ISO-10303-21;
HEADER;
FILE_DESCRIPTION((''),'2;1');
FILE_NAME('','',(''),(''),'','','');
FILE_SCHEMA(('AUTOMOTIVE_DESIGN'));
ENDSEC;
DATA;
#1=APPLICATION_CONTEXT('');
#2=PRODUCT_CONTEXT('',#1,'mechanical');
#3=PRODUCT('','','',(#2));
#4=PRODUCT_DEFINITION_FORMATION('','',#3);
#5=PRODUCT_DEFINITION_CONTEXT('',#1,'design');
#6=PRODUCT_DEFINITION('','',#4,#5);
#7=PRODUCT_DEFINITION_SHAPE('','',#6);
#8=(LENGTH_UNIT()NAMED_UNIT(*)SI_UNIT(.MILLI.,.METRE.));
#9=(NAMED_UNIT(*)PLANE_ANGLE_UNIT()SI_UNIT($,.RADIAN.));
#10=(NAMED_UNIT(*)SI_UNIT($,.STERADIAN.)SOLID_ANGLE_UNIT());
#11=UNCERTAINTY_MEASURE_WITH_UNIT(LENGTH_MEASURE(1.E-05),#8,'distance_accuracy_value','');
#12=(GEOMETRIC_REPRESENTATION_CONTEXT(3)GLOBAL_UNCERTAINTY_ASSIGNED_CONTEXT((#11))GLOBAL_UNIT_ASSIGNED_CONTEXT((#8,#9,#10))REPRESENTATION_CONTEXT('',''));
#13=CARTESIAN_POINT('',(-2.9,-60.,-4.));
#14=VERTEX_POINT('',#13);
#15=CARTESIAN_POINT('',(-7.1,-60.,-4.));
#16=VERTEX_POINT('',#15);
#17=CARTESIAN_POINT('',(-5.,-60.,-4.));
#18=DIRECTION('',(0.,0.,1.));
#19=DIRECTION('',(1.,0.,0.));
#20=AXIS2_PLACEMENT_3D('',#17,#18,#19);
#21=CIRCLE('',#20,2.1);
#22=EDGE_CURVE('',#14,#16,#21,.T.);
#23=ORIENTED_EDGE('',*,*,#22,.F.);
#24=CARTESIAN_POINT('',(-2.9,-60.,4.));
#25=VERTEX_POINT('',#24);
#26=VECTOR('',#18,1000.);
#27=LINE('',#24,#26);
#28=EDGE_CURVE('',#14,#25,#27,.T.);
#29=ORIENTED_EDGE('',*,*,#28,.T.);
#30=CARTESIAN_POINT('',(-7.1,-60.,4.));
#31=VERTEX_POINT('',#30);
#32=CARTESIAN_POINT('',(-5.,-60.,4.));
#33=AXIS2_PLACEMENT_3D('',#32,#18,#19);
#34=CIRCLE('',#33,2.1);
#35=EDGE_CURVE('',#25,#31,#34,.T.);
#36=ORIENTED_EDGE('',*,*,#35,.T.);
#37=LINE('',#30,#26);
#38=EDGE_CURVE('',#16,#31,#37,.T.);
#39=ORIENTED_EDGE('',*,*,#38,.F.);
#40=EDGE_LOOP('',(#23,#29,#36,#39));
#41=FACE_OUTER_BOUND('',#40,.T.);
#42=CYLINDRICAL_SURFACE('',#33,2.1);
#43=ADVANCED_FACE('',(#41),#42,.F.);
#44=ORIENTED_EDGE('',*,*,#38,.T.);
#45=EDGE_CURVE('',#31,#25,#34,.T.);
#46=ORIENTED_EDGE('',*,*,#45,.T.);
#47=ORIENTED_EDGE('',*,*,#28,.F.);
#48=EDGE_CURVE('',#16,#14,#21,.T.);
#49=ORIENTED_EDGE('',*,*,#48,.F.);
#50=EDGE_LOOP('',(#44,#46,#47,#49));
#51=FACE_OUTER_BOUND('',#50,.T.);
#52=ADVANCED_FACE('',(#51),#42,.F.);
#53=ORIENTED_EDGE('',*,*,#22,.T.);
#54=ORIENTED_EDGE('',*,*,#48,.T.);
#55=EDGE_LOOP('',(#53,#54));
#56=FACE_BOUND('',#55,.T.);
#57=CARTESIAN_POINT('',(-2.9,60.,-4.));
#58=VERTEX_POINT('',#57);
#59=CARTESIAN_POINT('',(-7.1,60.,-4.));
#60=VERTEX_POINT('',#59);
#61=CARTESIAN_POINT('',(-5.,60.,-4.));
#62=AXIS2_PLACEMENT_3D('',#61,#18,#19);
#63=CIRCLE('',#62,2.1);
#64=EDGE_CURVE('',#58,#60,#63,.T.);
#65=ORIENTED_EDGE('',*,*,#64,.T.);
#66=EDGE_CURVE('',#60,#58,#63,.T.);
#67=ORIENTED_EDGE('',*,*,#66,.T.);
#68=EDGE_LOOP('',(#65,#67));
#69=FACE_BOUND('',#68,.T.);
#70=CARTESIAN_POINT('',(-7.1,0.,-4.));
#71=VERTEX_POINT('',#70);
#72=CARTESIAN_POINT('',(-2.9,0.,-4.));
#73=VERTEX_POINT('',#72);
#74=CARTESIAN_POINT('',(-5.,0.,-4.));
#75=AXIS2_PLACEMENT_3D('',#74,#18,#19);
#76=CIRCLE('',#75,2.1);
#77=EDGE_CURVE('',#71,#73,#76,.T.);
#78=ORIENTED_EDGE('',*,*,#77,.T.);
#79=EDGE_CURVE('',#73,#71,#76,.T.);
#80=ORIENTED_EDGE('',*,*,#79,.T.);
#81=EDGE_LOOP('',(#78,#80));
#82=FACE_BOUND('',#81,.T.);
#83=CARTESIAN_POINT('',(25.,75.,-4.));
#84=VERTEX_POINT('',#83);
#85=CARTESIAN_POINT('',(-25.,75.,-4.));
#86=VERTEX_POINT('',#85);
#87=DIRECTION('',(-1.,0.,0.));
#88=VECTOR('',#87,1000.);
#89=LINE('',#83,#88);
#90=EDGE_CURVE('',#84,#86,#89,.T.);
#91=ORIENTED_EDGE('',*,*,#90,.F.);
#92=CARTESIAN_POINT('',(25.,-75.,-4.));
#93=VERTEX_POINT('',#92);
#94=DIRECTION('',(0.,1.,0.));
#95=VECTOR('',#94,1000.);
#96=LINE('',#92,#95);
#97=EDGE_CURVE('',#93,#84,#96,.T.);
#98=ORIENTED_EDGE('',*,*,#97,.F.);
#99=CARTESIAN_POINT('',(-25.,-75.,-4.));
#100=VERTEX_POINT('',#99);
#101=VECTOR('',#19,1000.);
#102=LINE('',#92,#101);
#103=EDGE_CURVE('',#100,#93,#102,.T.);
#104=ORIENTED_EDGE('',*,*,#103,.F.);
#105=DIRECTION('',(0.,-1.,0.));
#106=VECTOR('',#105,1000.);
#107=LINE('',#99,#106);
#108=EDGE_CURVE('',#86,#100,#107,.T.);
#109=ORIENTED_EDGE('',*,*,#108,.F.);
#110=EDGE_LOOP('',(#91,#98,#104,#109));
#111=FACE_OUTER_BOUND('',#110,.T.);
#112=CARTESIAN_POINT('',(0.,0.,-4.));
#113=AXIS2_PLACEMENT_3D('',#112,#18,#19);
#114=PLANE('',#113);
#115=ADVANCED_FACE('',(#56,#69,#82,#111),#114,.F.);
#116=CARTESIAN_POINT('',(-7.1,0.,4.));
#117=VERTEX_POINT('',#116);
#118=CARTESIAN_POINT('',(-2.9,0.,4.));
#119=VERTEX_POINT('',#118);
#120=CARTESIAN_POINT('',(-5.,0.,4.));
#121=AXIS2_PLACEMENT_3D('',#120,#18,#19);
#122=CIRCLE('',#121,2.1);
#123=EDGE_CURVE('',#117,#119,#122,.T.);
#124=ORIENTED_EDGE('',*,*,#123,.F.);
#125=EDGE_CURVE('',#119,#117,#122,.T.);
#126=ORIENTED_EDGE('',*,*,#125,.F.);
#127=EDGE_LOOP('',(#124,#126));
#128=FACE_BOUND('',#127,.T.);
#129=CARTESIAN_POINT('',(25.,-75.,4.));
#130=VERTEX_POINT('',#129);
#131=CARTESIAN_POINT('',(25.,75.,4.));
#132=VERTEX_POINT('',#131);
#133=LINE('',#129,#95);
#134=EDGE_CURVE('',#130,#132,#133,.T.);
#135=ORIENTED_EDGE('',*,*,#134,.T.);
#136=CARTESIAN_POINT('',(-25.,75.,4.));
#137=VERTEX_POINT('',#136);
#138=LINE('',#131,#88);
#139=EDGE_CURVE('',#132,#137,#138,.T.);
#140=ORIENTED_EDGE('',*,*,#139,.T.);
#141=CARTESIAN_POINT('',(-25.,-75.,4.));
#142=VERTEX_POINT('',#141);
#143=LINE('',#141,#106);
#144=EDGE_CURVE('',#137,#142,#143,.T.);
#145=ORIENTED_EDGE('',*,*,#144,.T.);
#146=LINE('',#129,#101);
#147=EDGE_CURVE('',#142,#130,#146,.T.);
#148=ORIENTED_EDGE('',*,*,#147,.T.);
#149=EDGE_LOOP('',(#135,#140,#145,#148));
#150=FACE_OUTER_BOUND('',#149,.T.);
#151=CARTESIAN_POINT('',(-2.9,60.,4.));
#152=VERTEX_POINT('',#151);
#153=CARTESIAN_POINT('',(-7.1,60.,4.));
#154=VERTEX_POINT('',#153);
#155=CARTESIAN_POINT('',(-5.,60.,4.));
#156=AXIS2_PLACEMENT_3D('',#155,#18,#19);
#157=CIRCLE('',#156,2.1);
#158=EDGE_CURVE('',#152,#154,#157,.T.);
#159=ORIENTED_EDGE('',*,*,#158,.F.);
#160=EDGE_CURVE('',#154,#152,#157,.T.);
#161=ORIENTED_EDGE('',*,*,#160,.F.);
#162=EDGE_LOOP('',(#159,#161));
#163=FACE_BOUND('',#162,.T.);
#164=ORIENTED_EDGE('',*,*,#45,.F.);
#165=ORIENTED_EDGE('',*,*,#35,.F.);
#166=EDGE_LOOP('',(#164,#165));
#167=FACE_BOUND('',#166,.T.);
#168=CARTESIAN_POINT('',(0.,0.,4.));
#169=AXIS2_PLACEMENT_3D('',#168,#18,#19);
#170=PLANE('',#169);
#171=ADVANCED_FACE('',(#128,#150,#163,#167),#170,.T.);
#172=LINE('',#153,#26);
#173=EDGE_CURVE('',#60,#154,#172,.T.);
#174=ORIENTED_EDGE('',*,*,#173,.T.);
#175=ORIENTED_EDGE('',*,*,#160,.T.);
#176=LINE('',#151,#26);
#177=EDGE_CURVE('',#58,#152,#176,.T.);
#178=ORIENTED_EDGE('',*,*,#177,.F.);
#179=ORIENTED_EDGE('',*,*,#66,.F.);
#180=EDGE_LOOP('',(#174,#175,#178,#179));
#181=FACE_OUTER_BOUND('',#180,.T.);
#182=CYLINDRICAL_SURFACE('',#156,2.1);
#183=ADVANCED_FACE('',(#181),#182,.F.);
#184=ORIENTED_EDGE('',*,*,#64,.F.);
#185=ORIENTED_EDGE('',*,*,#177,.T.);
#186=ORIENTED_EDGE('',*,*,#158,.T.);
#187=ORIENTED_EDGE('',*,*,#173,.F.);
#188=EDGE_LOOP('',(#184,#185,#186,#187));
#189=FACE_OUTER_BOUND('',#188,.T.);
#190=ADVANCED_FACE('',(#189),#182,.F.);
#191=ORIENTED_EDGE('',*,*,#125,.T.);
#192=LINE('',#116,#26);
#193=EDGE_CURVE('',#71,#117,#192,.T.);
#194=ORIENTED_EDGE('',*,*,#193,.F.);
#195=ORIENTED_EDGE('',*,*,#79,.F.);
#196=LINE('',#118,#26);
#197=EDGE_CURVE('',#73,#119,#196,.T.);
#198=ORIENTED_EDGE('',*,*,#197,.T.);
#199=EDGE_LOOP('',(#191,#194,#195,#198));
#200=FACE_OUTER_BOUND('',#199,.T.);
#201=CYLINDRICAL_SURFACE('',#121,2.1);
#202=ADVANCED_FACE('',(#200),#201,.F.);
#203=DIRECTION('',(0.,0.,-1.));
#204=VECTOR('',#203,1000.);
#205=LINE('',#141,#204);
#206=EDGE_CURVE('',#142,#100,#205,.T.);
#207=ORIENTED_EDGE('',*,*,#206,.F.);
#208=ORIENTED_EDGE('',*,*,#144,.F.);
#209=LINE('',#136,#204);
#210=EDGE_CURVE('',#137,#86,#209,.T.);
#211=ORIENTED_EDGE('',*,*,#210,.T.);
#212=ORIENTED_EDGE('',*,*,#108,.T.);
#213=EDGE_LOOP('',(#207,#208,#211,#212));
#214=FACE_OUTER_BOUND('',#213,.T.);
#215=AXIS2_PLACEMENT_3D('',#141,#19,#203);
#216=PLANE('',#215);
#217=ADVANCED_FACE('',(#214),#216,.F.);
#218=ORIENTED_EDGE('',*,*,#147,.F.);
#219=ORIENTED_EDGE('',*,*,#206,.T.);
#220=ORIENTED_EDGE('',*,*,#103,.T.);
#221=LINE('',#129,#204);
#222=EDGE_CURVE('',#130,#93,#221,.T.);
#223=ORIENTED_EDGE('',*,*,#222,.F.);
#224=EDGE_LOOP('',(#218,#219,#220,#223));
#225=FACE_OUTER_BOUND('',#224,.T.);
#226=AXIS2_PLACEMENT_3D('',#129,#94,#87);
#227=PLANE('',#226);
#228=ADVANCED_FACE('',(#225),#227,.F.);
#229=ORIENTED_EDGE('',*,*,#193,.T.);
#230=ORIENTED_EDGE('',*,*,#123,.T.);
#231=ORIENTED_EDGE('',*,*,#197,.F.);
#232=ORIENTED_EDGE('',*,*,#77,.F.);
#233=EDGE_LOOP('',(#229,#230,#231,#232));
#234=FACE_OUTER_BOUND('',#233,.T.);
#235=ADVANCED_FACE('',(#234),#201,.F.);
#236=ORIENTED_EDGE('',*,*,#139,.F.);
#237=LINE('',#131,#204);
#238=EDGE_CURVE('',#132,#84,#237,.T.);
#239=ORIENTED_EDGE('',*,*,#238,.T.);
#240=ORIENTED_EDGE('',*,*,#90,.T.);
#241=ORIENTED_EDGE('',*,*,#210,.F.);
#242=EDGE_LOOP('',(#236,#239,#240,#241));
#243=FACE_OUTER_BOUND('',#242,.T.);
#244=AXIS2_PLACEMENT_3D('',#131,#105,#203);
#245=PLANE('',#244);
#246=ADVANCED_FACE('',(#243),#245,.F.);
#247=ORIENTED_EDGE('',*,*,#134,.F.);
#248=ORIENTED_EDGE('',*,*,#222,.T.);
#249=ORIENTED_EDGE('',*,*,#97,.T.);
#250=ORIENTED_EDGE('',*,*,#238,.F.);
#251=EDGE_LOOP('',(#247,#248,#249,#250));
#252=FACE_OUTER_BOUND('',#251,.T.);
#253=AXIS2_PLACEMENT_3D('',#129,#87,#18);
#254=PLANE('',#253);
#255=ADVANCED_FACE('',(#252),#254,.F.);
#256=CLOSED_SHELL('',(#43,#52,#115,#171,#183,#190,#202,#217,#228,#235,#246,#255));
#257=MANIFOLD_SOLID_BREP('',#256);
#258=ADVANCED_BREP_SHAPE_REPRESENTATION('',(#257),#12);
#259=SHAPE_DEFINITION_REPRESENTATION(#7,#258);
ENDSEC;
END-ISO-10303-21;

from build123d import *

# Parameters (mm, degrees)
SKETCH1_W           = 50
SKETCH1_H           = 150
BOSS_EXTRUDE1_DEPTH = 4
M5_TAPPED_HOLE1_D   = 4.2


with BuildPart() as part:
    # Sketch1 → Boss-Extrude1 (new, symmetric)
    with BuildSketch(Plane.XY):
        Rectangle(SKETCH1_W, SKETCH1_H)
    extrude(amount=BOSS_EXTRUDE1_DEPTH, both=True)

    # M5 Tapped Hole1 (through all)
    with Locations(Plane.XY.offset(4)):
        with Locations((-5, 60), (-5, -60), (-5, 0)):
            Hole(M5_TAPPED_HOLE1_D / 2)


solid = part.part
